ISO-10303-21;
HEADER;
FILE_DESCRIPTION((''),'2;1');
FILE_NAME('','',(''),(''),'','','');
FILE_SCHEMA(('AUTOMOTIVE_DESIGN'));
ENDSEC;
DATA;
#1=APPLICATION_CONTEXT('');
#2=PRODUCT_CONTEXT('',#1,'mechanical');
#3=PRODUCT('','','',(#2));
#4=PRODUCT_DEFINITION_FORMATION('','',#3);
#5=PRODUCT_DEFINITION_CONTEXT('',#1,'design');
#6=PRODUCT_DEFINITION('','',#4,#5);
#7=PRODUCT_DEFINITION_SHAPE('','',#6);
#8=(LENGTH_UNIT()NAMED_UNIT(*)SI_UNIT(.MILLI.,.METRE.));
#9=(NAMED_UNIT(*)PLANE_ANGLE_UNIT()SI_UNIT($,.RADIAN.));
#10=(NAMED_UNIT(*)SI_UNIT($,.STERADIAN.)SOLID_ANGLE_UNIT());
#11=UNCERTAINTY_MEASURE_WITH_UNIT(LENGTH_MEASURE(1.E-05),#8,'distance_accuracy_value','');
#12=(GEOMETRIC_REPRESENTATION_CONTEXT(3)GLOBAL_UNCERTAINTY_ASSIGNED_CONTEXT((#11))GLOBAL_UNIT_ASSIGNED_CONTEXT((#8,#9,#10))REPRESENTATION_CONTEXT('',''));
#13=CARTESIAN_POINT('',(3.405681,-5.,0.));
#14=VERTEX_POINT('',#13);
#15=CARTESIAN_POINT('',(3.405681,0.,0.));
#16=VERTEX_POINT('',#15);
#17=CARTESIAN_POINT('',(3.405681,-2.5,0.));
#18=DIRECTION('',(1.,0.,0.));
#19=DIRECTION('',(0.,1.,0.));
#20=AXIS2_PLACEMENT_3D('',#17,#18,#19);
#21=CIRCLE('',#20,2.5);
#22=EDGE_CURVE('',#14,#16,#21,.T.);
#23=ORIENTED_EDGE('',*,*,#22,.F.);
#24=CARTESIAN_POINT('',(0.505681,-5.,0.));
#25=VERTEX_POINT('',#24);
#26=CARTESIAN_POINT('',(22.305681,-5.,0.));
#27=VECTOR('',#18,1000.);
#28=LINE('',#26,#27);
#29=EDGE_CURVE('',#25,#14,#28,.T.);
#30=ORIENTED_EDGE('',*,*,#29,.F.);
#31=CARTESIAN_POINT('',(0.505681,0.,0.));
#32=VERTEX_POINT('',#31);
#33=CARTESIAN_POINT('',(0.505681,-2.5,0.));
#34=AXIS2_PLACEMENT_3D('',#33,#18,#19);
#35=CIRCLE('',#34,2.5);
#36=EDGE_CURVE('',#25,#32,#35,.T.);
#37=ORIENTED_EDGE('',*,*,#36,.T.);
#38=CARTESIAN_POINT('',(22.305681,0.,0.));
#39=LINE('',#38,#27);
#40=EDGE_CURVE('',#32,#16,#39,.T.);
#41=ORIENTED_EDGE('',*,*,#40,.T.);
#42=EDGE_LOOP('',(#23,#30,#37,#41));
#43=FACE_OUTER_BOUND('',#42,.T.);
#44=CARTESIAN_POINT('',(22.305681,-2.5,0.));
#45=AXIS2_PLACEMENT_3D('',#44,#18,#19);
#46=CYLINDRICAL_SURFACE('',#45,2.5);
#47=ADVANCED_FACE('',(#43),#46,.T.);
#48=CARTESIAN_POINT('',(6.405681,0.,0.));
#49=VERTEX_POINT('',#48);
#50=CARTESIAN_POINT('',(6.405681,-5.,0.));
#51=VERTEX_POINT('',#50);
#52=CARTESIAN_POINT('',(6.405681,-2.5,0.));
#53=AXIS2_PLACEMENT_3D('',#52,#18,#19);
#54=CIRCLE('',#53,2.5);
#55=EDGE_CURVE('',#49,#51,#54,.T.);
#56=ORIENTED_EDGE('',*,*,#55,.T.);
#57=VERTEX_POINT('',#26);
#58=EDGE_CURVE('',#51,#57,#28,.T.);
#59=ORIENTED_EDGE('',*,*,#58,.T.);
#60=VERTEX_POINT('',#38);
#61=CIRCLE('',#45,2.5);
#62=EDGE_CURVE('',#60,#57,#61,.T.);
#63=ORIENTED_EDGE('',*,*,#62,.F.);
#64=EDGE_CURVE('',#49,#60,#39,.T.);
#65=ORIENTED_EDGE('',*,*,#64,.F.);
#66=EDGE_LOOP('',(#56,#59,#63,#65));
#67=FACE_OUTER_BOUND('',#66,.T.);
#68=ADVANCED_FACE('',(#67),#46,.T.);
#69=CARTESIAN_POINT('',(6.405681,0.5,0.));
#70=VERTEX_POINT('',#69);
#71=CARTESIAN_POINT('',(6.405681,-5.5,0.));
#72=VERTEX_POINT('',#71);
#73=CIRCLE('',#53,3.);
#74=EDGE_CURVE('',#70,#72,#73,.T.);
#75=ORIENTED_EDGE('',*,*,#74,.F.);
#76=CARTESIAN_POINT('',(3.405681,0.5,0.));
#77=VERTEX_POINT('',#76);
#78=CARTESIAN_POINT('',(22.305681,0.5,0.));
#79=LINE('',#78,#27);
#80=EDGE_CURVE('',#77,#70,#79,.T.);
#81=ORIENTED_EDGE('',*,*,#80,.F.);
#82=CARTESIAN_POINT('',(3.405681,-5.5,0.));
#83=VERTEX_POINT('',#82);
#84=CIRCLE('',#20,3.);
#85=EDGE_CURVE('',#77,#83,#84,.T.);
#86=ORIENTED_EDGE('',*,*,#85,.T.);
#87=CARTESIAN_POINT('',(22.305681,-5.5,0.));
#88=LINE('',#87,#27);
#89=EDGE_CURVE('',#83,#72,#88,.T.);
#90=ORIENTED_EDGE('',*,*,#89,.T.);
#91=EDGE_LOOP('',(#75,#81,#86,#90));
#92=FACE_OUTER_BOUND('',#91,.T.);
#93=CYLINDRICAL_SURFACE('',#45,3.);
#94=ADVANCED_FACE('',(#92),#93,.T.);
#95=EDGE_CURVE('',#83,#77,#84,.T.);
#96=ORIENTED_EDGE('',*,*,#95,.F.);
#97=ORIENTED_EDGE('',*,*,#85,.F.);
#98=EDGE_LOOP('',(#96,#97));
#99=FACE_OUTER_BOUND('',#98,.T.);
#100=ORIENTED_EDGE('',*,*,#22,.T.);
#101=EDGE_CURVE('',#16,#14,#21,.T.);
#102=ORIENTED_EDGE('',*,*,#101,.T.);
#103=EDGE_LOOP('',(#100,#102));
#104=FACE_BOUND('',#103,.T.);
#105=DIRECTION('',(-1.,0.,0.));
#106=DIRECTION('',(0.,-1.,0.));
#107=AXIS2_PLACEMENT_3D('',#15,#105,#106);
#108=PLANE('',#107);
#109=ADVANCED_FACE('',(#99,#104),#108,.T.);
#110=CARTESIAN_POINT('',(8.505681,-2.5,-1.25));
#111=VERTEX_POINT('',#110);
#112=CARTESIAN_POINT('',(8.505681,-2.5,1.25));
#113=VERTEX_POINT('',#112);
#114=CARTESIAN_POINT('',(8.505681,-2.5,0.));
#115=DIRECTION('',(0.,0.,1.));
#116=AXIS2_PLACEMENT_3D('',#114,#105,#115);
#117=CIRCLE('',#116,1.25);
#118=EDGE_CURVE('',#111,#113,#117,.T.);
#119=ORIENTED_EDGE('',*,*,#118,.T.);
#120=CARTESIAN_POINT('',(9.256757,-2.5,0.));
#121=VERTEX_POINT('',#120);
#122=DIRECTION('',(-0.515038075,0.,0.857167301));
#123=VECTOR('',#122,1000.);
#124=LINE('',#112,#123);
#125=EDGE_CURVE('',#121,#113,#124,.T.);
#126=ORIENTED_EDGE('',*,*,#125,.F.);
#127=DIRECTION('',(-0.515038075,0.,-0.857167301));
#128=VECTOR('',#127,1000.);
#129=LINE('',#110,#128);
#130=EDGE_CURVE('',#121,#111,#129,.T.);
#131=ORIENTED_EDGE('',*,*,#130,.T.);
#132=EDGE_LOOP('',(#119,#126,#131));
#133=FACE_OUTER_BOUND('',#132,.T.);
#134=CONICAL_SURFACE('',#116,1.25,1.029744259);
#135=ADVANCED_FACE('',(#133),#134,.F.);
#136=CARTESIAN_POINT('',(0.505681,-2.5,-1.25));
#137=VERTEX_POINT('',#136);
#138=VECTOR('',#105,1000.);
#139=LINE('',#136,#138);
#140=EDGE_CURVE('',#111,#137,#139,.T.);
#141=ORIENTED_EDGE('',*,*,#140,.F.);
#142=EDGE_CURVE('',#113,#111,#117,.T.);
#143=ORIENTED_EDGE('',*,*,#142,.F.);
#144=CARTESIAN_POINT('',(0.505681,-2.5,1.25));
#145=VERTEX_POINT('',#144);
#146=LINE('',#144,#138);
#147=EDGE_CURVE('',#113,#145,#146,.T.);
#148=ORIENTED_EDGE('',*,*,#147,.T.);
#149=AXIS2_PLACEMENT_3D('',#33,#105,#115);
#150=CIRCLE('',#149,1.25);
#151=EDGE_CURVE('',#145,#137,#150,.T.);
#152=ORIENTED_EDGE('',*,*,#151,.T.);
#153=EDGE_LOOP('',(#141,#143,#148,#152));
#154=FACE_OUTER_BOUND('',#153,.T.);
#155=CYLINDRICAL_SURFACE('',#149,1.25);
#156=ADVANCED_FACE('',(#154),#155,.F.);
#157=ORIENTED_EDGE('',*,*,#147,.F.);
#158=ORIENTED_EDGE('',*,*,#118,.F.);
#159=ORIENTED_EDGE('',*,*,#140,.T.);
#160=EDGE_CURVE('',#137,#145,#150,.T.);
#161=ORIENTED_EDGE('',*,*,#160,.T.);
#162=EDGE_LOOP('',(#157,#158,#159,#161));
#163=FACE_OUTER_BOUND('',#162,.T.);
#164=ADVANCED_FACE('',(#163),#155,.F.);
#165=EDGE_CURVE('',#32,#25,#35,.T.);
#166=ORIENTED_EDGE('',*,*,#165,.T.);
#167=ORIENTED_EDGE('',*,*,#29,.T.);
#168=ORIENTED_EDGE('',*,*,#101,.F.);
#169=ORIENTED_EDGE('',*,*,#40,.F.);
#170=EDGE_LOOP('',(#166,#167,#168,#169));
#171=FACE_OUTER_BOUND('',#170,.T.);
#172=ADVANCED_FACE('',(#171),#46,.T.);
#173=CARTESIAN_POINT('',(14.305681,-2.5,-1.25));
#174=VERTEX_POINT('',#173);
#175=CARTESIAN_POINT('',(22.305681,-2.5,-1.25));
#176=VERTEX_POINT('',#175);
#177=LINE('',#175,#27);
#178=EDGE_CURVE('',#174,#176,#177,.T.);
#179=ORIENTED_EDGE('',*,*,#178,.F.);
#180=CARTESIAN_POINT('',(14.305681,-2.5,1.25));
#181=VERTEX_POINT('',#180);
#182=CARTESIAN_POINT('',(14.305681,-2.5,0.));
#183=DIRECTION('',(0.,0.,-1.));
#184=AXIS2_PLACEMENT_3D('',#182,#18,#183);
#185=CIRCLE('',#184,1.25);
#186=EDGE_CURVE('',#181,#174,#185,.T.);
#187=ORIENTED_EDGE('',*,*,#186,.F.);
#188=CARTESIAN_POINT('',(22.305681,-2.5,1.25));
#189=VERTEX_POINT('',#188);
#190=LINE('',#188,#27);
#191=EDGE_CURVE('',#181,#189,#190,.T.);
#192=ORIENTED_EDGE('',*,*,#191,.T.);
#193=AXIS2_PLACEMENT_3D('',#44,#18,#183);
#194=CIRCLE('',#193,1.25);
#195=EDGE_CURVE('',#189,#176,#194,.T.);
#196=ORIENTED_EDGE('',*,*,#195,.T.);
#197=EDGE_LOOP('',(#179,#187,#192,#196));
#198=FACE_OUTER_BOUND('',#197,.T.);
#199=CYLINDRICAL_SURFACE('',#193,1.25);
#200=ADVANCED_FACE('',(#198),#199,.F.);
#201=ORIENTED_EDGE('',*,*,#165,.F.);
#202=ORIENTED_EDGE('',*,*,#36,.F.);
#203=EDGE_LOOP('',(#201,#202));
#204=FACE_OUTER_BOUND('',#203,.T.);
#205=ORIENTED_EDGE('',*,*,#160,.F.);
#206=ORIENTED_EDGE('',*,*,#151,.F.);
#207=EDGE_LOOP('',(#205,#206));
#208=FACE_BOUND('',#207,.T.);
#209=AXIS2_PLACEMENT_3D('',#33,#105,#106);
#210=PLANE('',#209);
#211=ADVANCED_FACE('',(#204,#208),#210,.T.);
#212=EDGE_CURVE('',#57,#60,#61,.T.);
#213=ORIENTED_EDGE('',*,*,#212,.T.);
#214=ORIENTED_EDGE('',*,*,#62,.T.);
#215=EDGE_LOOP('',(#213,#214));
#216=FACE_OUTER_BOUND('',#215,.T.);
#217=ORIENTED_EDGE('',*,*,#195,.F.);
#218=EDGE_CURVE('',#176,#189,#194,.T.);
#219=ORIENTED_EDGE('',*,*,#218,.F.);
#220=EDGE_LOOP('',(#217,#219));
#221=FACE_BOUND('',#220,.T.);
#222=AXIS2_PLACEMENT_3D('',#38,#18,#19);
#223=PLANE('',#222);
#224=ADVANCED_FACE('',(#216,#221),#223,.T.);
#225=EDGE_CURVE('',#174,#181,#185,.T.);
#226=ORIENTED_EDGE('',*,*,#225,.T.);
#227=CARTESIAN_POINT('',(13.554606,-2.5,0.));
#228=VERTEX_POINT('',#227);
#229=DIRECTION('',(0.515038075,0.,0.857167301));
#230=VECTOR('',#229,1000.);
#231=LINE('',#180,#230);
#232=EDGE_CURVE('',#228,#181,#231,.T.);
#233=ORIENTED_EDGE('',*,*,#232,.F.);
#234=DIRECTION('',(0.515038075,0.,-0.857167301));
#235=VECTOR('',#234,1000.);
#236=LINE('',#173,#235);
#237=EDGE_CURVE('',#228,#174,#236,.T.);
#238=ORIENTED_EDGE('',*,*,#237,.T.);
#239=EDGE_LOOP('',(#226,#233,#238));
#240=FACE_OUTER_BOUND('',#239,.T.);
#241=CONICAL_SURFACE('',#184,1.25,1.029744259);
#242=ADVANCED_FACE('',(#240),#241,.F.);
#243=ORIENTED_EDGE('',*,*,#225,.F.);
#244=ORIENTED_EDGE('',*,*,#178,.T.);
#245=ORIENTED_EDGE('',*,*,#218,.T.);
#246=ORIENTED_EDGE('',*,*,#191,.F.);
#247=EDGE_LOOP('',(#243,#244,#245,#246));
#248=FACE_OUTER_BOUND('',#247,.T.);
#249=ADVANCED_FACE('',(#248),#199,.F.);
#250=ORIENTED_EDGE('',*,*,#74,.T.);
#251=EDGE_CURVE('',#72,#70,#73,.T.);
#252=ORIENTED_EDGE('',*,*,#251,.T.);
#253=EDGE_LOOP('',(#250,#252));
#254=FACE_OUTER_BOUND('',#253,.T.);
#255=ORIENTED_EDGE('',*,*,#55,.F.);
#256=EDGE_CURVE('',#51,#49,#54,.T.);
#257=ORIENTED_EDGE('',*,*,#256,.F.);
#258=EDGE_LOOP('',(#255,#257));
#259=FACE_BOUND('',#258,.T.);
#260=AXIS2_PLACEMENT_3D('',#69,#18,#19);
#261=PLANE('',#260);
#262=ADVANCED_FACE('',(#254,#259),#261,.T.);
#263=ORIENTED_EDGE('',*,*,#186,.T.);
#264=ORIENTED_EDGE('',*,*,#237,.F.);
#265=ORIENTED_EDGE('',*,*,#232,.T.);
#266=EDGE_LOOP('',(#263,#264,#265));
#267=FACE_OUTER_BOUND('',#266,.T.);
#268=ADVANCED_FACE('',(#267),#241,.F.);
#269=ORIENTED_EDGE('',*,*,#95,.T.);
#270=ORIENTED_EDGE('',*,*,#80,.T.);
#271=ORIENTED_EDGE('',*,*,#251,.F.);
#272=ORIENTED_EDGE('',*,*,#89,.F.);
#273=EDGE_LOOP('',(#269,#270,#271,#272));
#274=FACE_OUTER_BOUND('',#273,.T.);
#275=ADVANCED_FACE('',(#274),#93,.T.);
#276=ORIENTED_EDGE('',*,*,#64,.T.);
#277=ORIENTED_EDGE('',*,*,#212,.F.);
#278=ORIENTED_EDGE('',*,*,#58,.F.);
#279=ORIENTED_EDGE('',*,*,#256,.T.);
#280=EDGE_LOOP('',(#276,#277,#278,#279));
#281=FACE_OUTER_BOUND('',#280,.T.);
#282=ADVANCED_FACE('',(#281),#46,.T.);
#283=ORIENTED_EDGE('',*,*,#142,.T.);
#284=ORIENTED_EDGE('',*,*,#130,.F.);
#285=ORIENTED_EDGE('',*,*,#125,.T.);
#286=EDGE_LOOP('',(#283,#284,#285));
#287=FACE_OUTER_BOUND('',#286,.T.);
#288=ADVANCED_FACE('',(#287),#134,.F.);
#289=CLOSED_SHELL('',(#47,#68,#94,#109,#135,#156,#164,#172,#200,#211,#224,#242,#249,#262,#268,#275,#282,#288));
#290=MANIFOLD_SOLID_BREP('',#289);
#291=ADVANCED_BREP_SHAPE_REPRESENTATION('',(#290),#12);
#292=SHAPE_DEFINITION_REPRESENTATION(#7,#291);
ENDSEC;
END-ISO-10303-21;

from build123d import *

# Parameters (mm, degrees)
M3_TAPPED_HOLE1_D               = 2.5
M3_TAPPED_HOLE1_DEPTH           = 8
M3_TAPPED_HOLE1_TIP             = 0.751075774
M3_TAPPED_HOLE1_ON_FACE_2_D     = 2.5
M3_TAPPED_HOLE1_ON_FACE_2_DEPTH = 8
M3_TAPPED_HOLE1_ON_FACE_2_TIP   = 0.751075774


with BuildPart() as part:
    # Sketch1 → Revolve1 (revolve)
    with BuildSketch(Plane.XY):
        Polygon((22.305681316, -2.5), (0.505681316, -2.5), (0.505681316, 0), (3.405681316, 0), (3.405681316, 0.5), (6.405681316, 0.5), (6.405681316, 0), (22.305681316, 0), align=None)
    revolve(axis=Axis((22.305681316, -2.5, 0), (-1, 0, 0)))

    # M3 Tapped Hole1
    with Locations(Plane(origin=(0.505681316, -2.5, 0), x_dir=(0, 0, -1), z_dir=(-1, 0, 0))):
        with Locations((0, 0)):
            Hole(M3_TAPPED_HOLE1_D / 2, depth=M3_TAPPED_HOLE1_DEPTH)
            with Locations((0, 0, -(M3_TAPPED_HOLE1_DEPTH + M3_TAPPED_HOLE1_TIP / 2))):  # 118° drill point
                Cone(0, M3_TAPPED_HOLE1_D / 2, M3_TAPPED_HOLE1_TIP, mode=Mode.SUBTRACT)

    # M3 Tapped Hole1 on face 2
    with Locations(Plane(origin=(22.305681316, -2.5, 0), x_dir=(0, 0, 1), z_dir=(1, 0, 0))):
        with Locations((0, 0)):
            Hole(M3_TAPPED_HOLE1_ON_FACE_2_D / 2, depth=M3_TAPPED_HOLE1_ON_FACE_2_DEPTH)
            with Locations((0, 0, -(M3_TAPPED_HOLE1_ON_FACE_2_DEPTH + M3_TAPPED_HOLE1_ON_FACE_2_TIP / 2))):  # 118° drill point
                Cone(0, M3_TAPPED_HOLE1_ON_FACE_2_D / 2, M3_TAPPED_HOLE1_ON_FACE_2_TIP, mode=Mode.SUBTRACT)


solid = part.part
